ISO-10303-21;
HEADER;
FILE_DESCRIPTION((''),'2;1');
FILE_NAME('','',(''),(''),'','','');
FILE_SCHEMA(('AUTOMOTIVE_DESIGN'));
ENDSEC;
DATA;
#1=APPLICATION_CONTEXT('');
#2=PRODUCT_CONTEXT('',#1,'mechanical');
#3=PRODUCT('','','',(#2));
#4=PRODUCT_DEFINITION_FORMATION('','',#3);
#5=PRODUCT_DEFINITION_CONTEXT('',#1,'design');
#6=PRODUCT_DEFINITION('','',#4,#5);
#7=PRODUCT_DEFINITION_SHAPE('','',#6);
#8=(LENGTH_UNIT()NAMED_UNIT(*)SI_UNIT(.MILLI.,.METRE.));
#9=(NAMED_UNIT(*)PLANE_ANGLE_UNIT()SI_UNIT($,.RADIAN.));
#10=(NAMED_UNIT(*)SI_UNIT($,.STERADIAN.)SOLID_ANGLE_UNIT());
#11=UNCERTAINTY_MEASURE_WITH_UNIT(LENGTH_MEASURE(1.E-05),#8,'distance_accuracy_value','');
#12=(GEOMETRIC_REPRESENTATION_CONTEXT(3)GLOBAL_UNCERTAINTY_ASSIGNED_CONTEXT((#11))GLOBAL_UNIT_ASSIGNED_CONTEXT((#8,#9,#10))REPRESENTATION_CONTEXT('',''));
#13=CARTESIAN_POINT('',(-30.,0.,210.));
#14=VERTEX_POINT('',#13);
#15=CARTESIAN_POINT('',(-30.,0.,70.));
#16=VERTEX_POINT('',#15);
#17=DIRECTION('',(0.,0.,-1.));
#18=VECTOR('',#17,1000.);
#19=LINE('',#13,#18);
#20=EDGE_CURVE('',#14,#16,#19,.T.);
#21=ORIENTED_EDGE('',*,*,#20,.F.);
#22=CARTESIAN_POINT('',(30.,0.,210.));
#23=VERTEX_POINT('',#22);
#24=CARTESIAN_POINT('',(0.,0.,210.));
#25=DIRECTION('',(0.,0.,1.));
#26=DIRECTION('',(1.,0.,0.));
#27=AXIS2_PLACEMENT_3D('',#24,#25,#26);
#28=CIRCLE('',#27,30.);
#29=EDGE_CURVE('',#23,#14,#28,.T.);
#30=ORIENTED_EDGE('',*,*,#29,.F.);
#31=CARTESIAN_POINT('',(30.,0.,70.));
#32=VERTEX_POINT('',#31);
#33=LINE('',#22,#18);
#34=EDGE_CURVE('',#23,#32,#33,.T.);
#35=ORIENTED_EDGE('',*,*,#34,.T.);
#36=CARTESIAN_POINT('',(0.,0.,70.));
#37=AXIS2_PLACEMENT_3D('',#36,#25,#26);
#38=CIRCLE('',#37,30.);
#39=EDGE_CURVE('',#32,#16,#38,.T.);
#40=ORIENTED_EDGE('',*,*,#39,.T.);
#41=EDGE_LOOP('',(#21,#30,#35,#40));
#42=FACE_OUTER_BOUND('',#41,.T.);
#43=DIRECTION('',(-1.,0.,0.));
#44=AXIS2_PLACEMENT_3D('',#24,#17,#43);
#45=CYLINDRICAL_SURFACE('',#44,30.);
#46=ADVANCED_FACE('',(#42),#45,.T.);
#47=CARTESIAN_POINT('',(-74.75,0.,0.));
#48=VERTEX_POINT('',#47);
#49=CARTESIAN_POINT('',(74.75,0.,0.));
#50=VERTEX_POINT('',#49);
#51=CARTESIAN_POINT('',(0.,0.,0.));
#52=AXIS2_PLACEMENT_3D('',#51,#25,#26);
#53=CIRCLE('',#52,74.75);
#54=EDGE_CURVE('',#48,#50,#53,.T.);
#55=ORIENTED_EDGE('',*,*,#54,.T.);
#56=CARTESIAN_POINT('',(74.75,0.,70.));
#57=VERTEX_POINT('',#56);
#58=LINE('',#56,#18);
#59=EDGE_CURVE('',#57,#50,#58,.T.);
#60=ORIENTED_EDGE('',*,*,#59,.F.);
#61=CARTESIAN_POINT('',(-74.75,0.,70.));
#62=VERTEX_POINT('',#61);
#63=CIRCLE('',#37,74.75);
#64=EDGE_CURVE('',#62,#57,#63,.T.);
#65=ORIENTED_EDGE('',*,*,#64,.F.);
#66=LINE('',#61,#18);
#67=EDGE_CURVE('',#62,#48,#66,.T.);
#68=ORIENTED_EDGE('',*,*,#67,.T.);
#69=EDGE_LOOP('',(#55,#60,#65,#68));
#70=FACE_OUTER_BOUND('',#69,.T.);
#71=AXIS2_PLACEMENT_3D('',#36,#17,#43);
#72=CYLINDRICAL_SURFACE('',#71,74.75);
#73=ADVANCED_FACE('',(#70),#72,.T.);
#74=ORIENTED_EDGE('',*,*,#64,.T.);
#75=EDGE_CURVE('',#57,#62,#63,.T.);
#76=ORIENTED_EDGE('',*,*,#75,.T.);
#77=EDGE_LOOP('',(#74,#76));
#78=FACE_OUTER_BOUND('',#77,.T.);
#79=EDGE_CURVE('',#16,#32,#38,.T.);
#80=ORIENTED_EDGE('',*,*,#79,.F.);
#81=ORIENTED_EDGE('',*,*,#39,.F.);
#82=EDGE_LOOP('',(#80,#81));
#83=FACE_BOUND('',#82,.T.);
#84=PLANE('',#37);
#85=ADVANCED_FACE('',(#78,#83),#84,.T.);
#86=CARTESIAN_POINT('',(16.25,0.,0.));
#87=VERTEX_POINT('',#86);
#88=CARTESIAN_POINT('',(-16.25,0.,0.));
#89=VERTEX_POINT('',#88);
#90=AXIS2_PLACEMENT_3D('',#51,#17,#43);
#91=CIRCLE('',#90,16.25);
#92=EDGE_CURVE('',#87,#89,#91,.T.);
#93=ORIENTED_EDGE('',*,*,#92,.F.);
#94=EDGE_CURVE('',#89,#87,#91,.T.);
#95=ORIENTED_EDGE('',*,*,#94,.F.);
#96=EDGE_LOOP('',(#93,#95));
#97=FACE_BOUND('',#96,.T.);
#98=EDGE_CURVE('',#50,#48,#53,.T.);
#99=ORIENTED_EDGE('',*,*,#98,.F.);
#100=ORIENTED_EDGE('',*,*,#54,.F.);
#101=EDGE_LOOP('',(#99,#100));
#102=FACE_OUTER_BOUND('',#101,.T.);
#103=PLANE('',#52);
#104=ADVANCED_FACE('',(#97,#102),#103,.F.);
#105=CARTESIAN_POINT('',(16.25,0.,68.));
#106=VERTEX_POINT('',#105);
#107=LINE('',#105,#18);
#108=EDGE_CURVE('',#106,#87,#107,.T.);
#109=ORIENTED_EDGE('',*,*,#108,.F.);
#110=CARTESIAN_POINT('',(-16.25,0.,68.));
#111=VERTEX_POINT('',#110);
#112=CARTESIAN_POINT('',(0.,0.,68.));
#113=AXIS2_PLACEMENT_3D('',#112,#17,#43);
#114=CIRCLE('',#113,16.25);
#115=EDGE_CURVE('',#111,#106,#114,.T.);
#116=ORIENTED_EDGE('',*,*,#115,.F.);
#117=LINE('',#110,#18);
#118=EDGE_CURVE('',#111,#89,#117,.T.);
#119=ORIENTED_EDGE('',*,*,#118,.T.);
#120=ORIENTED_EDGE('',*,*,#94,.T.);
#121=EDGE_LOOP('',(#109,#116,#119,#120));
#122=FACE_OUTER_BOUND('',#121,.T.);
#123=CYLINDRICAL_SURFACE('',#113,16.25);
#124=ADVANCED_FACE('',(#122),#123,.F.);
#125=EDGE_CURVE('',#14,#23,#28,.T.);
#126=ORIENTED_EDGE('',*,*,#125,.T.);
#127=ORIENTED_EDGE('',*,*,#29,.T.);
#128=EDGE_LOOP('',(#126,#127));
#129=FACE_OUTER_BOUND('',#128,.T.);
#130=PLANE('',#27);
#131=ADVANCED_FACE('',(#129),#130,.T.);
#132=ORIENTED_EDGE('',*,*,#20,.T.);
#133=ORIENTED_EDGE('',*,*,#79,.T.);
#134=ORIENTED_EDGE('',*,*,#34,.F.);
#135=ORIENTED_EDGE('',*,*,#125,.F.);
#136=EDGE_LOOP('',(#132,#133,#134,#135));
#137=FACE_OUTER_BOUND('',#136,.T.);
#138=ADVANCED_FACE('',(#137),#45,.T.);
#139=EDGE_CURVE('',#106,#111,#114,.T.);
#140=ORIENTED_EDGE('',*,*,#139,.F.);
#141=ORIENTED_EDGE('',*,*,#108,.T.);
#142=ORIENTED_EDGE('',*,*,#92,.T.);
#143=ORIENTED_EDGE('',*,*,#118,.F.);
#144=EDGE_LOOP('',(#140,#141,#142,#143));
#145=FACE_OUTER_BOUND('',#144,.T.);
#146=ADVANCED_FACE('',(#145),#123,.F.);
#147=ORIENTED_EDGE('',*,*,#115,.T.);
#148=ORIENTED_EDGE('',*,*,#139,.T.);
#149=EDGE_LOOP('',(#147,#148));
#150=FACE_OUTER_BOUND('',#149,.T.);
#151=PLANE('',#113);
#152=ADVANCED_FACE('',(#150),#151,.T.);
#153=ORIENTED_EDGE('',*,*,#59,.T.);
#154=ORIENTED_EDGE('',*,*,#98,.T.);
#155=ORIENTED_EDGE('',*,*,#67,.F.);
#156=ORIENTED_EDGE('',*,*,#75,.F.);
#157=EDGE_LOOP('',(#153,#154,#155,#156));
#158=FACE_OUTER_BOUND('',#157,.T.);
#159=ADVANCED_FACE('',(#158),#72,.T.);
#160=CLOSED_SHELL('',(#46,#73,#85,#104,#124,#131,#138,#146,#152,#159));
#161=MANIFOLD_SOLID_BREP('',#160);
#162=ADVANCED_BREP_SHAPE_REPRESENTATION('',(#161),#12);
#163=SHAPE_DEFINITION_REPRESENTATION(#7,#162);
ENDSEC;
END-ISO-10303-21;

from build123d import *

# Parameters (mm, degrees)
SKETCH_1_R          = 74.75
EXTRUDE_1_DEPTH     = 70
SKETCH_2_R          = 16.25
CUT_EXTRUDE_1_DEPTH = 68
SKETCH_3_R          = 30
EXTRUDE_2_DEPTH     = 140


with BuildPart() as part:
    # 草图1 → 凸台-拉伸1 (new body)
    with BuildSketch(Plane.XY):
        Circle(SKETCH_1_R)
    extrude(amount=EXTRUDE_1_DEPTH)

    # 草图2 → 切除-拉伸1 (cut)
    with BuildSketch(Plane(origin=(0, 0, 0), x_dir=(-1, 0, 0), z_dir=(0, 0, -1))):
        Circle(SKETCH_2_R)
    extrude(amount=-CUT_EXTRUDE_1_DEPTH, mode=Mode.SUBTRACT)

    # 草图3 → 凸台-拉伸2 (add)
    with BuildSketch(Plane.XY.offset(70)):
        Circle(SKETCH_3_R)
    extrude(amount=EXTRUDE_2_DEPTH)


solid = part.part
